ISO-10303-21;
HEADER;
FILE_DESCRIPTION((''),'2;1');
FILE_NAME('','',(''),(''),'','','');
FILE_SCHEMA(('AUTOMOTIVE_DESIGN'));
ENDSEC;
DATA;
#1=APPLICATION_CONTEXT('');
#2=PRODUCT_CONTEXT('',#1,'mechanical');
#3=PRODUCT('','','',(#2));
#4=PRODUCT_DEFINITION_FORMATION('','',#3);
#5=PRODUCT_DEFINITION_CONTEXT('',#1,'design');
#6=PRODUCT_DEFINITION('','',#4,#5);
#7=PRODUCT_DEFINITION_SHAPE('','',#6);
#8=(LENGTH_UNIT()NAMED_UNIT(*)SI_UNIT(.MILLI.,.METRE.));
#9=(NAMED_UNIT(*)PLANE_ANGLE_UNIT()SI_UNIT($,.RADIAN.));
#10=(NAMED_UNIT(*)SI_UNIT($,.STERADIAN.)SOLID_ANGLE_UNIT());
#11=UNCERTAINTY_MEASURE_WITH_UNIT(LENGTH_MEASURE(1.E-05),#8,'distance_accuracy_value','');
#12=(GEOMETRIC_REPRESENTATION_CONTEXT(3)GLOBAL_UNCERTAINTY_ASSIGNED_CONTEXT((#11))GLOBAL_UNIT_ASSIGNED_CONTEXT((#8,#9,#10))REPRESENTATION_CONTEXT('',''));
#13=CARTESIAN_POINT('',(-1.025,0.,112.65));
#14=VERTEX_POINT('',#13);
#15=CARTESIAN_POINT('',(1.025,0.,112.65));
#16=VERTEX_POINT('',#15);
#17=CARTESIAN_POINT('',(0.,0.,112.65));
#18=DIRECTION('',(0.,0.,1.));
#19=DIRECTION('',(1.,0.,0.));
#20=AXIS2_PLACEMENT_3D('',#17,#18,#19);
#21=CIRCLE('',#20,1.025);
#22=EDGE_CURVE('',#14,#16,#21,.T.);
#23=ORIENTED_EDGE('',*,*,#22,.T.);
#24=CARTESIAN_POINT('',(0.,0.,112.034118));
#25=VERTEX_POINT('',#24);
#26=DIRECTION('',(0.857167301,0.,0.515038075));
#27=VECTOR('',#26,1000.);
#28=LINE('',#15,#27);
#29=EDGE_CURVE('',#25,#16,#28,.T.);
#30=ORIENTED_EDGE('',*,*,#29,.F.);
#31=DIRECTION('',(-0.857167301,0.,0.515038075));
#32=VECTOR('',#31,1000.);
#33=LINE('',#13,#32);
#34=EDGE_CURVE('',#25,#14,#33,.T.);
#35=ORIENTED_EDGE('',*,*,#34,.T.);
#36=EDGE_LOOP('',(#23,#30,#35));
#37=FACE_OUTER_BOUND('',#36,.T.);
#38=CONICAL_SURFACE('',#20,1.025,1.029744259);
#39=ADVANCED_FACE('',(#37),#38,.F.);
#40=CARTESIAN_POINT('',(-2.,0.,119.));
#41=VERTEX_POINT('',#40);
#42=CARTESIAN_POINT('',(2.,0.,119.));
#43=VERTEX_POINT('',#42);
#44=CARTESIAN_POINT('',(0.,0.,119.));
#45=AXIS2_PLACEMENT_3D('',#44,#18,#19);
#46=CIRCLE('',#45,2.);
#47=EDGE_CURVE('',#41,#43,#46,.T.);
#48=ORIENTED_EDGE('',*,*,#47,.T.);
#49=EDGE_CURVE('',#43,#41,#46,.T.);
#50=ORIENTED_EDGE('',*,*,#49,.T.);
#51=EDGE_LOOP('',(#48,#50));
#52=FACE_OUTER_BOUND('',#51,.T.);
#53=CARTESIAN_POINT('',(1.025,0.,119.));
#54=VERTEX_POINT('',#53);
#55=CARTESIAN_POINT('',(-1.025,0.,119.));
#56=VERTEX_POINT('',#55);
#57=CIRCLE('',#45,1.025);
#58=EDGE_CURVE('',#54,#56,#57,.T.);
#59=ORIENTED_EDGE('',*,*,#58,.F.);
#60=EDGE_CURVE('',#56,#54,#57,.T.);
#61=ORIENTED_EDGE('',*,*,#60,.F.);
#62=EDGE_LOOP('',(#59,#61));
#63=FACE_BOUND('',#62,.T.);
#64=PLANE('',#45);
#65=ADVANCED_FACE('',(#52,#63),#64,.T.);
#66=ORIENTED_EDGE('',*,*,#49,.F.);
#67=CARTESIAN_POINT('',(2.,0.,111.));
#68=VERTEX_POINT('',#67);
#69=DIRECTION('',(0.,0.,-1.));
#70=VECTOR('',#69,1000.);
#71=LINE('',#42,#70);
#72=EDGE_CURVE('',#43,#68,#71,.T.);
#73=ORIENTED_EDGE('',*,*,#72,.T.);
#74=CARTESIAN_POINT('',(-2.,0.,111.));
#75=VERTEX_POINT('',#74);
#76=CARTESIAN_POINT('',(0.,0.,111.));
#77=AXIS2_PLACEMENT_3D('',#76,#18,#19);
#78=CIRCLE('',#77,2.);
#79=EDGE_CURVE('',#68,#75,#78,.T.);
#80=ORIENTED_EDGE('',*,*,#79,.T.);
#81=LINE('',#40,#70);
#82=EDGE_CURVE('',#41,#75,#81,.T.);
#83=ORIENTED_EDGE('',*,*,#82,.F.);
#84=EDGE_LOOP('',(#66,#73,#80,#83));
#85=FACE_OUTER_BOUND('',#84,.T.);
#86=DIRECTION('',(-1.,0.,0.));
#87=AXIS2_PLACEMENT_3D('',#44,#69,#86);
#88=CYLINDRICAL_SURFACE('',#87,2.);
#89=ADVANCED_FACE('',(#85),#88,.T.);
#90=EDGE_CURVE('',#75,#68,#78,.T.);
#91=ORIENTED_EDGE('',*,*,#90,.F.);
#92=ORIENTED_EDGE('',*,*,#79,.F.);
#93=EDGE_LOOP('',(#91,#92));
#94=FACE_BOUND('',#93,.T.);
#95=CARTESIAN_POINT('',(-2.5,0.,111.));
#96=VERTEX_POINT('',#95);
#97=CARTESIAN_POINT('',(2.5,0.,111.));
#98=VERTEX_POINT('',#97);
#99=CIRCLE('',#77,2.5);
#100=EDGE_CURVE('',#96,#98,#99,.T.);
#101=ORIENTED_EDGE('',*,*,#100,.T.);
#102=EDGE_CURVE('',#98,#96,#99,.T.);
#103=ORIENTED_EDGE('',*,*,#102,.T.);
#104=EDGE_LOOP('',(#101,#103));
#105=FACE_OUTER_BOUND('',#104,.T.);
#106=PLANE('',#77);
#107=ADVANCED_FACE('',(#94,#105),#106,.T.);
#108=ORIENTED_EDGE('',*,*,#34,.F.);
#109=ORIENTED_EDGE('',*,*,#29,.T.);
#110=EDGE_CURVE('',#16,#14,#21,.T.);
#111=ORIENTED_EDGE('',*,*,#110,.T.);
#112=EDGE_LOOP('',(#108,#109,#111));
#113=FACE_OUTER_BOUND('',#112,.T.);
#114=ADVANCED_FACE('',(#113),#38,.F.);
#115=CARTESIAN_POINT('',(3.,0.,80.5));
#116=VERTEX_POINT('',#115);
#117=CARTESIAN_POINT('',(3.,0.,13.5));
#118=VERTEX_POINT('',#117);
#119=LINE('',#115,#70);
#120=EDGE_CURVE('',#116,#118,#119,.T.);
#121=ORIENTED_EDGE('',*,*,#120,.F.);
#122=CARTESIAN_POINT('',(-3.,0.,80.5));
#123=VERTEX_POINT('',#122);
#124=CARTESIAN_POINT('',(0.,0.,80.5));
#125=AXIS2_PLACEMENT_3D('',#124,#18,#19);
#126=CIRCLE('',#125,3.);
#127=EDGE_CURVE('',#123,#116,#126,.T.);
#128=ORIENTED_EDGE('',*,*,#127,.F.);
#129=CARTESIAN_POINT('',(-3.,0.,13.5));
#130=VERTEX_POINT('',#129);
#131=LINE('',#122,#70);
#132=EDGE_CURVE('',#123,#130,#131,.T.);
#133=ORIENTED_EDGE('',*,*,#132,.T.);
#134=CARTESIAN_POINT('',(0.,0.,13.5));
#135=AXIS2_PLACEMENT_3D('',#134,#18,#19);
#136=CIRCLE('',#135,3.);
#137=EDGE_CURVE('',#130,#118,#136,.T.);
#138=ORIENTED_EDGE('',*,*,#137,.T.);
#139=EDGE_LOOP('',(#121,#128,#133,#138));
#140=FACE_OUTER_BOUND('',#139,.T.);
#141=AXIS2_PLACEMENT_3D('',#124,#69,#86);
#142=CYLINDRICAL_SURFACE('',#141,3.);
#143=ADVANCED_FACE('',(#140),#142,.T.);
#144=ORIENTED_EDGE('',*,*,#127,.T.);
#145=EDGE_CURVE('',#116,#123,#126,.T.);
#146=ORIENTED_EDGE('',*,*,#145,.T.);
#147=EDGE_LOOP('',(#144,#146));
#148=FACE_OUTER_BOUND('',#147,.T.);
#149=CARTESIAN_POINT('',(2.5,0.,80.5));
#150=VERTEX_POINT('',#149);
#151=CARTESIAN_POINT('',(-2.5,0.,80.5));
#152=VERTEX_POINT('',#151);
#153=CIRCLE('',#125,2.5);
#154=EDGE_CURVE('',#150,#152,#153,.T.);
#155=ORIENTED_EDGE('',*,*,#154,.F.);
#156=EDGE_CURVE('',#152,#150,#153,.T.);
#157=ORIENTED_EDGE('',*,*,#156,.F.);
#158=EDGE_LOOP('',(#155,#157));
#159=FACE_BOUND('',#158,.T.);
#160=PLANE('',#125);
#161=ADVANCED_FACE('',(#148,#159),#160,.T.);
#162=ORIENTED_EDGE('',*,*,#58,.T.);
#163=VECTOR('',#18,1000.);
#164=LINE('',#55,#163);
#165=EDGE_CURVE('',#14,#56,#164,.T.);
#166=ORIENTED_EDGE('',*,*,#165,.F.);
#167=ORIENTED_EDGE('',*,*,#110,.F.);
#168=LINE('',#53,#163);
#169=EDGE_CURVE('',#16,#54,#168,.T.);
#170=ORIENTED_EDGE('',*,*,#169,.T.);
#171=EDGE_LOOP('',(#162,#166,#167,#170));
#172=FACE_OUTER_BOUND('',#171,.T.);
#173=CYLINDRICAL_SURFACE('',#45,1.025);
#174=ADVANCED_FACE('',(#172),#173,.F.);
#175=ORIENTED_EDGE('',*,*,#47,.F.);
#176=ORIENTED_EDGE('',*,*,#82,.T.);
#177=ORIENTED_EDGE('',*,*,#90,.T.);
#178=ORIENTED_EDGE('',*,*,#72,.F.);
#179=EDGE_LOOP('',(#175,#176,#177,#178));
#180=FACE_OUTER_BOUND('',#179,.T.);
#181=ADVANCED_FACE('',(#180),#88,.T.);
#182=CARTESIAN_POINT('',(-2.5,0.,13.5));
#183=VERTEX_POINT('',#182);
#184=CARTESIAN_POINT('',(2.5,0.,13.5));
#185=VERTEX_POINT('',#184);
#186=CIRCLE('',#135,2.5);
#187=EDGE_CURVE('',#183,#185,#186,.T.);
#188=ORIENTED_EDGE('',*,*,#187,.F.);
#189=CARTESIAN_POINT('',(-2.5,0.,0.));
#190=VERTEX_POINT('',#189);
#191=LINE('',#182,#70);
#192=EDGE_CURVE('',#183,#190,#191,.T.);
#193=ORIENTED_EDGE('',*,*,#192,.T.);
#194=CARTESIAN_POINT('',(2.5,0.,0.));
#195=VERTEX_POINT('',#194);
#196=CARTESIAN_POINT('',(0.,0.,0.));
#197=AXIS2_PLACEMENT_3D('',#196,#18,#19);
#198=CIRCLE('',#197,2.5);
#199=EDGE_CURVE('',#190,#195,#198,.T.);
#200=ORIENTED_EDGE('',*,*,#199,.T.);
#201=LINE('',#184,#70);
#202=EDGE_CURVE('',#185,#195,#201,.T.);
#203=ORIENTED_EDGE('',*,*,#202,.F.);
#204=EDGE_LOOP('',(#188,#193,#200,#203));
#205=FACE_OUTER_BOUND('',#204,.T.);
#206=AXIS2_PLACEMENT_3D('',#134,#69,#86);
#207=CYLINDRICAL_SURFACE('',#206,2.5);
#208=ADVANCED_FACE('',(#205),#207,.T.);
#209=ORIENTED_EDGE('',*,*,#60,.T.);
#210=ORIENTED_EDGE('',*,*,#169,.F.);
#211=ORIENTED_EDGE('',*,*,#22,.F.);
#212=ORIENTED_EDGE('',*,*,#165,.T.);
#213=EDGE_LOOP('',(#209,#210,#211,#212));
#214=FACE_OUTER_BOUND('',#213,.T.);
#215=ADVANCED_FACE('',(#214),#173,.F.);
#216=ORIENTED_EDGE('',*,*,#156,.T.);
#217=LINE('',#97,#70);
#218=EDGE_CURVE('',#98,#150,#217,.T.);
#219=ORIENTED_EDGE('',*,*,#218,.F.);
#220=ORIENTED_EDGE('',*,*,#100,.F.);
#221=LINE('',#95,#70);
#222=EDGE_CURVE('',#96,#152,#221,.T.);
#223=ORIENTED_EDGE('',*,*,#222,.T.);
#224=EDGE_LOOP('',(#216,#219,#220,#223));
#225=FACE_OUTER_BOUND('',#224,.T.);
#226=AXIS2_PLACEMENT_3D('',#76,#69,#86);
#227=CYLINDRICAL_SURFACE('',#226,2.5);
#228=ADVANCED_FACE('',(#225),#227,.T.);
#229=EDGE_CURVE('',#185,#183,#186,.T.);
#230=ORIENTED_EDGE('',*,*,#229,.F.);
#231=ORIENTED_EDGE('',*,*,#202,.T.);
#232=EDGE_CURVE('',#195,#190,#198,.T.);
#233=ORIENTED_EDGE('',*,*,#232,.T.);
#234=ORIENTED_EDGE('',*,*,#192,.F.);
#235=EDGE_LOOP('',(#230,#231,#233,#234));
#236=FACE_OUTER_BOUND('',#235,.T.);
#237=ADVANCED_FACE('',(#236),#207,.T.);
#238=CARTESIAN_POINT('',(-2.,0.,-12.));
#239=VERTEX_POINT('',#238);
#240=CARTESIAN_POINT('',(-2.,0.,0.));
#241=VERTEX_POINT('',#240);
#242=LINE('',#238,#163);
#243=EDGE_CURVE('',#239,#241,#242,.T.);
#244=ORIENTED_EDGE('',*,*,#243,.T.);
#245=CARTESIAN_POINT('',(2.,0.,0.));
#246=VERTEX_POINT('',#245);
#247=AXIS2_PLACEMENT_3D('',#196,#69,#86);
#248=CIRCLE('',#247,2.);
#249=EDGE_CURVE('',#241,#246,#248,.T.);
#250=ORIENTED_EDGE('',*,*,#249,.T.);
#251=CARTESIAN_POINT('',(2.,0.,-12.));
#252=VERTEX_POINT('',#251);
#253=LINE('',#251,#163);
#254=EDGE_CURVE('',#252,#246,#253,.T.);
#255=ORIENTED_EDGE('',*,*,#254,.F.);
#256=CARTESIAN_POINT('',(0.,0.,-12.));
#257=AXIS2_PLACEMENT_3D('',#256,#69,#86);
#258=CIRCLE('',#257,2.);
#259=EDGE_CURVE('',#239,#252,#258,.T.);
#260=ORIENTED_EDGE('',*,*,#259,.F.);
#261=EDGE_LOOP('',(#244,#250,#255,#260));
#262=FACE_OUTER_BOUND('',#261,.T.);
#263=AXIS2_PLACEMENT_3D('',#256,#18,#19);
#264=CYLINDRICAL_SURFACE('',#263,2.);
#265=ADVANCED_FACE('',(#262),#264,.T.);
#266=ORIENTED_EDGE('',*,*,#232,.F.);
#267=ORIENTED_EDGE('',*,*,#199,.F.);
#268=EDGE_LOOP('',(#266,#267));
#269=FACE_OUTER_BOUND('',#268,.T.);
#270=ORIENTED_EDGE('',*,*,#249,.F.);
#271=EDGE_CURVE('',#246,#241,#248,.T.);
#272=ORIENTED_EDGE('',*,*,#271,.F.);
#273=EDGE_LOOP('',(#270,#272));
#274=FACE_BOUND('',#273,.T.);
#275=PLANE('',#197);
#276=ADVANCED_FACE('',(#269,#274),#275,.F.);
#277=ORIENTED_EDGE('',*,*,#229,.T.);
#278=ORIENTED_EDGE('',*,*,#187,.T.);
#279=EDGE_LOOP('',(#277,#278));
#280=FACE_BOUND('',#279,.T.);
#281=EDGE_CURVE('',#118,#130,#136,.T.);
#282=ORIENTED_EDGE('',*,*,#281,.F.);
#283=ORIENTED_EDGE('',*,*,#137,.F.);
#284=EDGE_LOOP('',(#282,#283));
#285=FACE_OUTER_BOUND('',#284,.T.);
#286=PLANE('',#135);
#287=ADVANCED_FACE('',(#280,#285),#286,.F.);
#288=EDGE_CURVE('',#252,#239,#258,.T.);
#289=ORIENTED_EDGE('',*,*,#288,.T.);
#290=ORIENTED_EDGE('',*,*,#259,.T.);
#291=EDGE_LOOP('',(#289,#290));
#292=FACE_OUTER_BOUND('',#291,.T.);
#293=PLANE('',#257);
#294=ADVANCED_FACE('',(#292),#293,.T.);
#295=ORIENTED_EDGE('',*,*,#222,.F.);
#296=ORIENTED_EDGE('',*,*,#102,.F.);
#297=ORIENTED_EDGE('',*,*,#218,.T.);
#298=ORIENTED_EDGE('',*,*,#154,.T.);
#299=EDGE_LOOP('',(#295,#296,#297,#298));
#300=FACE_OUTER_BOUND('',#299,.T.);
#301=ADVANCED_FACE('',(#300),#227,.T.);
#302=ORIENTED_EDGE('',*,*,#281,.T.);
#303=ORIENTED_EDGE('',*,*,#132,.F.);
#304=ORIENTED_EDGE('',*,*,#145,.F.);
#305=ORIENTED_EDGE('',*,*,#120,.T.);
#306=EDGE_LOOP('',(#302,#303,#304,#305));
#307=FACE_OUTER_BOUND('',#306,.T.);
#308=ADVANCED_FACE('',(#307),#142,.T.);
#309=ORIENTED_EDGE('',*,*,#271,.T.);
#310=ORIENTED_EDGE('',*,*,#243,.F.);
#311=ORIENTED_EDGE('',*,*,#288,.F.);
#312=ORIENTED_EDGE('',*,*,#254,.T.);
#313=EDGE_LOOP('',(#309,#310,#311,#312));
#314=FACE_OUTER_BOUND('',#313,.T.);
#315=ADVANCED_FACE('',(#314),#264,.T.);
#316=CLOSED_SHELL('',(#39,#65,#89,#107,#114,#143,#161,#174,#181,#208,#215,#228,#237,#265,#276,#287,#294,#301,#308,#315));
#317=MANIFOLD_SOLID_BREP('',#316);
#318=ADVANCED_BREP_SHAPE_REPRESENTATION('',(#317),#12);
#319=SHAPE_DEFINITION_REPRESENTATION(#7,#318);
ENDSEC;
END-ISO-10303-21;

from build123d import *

# Parameters (mm, degrees)
SKETCH1_R               = 2.5
BOSS_EXTRUDE1_DEPTH     = 13.5
SKETCH2_R               = 3
BOSS_EXTRUDE2_DEPTH     = 67
SKETCH3_R               = 2.5
BOSS_EXTRUDE3_DEPTH     = 30.5
SKETCH4_R               = 2
BOSS_EXTRUDE4_DEPTH     = 8
BOSS_EXTRUDE5_START     = 12
SKETCH5_R               = 2
BOSS_EXTRUDE5_DEPTH     = 12
M2_5_TAPPED_HOLE1_D     = 2.05
M2_5_TAPPED_HOLE1_DEPTH = 6.35
M2_5_TAPPED_HOLE1_TIP   = 0.615882135


with BuildPart() as part:
    # Sketch1 → Boss-Extrude1 (new body)
    with BuildSketch(Plane.XY):
        Circle(SKETCH1_R)
    extrude(amount=BOSS_EXTRUDE1_DEPTH)

    # Sketch2 → Boss-Extrude2 (add)
    with BuildSketch(Plane.XY.offset(13.5)):
        Circle(SKETCH2_R)
    extrude(amount=BOSS_EXTRUDE2_DEPTH)

    # Sketch3 → Boss-Extrude3 (add)
    with BuildSketch(Plane.XY.offset(80.5)):
        Circle(SKETCH3_R)
    extrude(amount=BOSS_EXTRUDE3_DEPTH)

    # Sketch4 → Boss-Extrude4 (add)
    with BuildSketch(Plane.XY.offset(111)):
        Circle(SKETCH4_R)
    extrude(amount=BOSS_EXTRUDE4_DEPTH)

    # Sketch5 → Boss-Extrude5 (add)
    with BuildSketch(Plane(origin=(0, 0, 0), x_dir=(-1, 0, 0), z_dir=(0, 0, -1)).offset(BOSS_EXTRUDE5_START)):
        with Locations(Location((0, 0, 0), (0, 0, 180))):
            Circle(SKETCH5_R)
    extrude(amount=-BOSS_EXTRUDE5_DEPTH)

    # M2.5 Tapped Hole1
    with Locations(Plane.XY.offset(119)):
        with Locations((0, 0)):
            Hole(M2_5_TAPPED_HOLE1_D / 2, depth=M2_5_TAPPED_HOLE1_DEPTH)
            with Locations((0, 0, -(M2_5_TAPPED_HOLE1_DEPTH + M2_5_TAPPED_HOLE1_TIP / 2))):  # 118° drill point
                Cone(0, M2_5_TAPPED_HOLE1_D / 2, M2_5_TAPPED_HOLE1_TIP, mode=Mode.SUBTRACT)


solid = part.part
